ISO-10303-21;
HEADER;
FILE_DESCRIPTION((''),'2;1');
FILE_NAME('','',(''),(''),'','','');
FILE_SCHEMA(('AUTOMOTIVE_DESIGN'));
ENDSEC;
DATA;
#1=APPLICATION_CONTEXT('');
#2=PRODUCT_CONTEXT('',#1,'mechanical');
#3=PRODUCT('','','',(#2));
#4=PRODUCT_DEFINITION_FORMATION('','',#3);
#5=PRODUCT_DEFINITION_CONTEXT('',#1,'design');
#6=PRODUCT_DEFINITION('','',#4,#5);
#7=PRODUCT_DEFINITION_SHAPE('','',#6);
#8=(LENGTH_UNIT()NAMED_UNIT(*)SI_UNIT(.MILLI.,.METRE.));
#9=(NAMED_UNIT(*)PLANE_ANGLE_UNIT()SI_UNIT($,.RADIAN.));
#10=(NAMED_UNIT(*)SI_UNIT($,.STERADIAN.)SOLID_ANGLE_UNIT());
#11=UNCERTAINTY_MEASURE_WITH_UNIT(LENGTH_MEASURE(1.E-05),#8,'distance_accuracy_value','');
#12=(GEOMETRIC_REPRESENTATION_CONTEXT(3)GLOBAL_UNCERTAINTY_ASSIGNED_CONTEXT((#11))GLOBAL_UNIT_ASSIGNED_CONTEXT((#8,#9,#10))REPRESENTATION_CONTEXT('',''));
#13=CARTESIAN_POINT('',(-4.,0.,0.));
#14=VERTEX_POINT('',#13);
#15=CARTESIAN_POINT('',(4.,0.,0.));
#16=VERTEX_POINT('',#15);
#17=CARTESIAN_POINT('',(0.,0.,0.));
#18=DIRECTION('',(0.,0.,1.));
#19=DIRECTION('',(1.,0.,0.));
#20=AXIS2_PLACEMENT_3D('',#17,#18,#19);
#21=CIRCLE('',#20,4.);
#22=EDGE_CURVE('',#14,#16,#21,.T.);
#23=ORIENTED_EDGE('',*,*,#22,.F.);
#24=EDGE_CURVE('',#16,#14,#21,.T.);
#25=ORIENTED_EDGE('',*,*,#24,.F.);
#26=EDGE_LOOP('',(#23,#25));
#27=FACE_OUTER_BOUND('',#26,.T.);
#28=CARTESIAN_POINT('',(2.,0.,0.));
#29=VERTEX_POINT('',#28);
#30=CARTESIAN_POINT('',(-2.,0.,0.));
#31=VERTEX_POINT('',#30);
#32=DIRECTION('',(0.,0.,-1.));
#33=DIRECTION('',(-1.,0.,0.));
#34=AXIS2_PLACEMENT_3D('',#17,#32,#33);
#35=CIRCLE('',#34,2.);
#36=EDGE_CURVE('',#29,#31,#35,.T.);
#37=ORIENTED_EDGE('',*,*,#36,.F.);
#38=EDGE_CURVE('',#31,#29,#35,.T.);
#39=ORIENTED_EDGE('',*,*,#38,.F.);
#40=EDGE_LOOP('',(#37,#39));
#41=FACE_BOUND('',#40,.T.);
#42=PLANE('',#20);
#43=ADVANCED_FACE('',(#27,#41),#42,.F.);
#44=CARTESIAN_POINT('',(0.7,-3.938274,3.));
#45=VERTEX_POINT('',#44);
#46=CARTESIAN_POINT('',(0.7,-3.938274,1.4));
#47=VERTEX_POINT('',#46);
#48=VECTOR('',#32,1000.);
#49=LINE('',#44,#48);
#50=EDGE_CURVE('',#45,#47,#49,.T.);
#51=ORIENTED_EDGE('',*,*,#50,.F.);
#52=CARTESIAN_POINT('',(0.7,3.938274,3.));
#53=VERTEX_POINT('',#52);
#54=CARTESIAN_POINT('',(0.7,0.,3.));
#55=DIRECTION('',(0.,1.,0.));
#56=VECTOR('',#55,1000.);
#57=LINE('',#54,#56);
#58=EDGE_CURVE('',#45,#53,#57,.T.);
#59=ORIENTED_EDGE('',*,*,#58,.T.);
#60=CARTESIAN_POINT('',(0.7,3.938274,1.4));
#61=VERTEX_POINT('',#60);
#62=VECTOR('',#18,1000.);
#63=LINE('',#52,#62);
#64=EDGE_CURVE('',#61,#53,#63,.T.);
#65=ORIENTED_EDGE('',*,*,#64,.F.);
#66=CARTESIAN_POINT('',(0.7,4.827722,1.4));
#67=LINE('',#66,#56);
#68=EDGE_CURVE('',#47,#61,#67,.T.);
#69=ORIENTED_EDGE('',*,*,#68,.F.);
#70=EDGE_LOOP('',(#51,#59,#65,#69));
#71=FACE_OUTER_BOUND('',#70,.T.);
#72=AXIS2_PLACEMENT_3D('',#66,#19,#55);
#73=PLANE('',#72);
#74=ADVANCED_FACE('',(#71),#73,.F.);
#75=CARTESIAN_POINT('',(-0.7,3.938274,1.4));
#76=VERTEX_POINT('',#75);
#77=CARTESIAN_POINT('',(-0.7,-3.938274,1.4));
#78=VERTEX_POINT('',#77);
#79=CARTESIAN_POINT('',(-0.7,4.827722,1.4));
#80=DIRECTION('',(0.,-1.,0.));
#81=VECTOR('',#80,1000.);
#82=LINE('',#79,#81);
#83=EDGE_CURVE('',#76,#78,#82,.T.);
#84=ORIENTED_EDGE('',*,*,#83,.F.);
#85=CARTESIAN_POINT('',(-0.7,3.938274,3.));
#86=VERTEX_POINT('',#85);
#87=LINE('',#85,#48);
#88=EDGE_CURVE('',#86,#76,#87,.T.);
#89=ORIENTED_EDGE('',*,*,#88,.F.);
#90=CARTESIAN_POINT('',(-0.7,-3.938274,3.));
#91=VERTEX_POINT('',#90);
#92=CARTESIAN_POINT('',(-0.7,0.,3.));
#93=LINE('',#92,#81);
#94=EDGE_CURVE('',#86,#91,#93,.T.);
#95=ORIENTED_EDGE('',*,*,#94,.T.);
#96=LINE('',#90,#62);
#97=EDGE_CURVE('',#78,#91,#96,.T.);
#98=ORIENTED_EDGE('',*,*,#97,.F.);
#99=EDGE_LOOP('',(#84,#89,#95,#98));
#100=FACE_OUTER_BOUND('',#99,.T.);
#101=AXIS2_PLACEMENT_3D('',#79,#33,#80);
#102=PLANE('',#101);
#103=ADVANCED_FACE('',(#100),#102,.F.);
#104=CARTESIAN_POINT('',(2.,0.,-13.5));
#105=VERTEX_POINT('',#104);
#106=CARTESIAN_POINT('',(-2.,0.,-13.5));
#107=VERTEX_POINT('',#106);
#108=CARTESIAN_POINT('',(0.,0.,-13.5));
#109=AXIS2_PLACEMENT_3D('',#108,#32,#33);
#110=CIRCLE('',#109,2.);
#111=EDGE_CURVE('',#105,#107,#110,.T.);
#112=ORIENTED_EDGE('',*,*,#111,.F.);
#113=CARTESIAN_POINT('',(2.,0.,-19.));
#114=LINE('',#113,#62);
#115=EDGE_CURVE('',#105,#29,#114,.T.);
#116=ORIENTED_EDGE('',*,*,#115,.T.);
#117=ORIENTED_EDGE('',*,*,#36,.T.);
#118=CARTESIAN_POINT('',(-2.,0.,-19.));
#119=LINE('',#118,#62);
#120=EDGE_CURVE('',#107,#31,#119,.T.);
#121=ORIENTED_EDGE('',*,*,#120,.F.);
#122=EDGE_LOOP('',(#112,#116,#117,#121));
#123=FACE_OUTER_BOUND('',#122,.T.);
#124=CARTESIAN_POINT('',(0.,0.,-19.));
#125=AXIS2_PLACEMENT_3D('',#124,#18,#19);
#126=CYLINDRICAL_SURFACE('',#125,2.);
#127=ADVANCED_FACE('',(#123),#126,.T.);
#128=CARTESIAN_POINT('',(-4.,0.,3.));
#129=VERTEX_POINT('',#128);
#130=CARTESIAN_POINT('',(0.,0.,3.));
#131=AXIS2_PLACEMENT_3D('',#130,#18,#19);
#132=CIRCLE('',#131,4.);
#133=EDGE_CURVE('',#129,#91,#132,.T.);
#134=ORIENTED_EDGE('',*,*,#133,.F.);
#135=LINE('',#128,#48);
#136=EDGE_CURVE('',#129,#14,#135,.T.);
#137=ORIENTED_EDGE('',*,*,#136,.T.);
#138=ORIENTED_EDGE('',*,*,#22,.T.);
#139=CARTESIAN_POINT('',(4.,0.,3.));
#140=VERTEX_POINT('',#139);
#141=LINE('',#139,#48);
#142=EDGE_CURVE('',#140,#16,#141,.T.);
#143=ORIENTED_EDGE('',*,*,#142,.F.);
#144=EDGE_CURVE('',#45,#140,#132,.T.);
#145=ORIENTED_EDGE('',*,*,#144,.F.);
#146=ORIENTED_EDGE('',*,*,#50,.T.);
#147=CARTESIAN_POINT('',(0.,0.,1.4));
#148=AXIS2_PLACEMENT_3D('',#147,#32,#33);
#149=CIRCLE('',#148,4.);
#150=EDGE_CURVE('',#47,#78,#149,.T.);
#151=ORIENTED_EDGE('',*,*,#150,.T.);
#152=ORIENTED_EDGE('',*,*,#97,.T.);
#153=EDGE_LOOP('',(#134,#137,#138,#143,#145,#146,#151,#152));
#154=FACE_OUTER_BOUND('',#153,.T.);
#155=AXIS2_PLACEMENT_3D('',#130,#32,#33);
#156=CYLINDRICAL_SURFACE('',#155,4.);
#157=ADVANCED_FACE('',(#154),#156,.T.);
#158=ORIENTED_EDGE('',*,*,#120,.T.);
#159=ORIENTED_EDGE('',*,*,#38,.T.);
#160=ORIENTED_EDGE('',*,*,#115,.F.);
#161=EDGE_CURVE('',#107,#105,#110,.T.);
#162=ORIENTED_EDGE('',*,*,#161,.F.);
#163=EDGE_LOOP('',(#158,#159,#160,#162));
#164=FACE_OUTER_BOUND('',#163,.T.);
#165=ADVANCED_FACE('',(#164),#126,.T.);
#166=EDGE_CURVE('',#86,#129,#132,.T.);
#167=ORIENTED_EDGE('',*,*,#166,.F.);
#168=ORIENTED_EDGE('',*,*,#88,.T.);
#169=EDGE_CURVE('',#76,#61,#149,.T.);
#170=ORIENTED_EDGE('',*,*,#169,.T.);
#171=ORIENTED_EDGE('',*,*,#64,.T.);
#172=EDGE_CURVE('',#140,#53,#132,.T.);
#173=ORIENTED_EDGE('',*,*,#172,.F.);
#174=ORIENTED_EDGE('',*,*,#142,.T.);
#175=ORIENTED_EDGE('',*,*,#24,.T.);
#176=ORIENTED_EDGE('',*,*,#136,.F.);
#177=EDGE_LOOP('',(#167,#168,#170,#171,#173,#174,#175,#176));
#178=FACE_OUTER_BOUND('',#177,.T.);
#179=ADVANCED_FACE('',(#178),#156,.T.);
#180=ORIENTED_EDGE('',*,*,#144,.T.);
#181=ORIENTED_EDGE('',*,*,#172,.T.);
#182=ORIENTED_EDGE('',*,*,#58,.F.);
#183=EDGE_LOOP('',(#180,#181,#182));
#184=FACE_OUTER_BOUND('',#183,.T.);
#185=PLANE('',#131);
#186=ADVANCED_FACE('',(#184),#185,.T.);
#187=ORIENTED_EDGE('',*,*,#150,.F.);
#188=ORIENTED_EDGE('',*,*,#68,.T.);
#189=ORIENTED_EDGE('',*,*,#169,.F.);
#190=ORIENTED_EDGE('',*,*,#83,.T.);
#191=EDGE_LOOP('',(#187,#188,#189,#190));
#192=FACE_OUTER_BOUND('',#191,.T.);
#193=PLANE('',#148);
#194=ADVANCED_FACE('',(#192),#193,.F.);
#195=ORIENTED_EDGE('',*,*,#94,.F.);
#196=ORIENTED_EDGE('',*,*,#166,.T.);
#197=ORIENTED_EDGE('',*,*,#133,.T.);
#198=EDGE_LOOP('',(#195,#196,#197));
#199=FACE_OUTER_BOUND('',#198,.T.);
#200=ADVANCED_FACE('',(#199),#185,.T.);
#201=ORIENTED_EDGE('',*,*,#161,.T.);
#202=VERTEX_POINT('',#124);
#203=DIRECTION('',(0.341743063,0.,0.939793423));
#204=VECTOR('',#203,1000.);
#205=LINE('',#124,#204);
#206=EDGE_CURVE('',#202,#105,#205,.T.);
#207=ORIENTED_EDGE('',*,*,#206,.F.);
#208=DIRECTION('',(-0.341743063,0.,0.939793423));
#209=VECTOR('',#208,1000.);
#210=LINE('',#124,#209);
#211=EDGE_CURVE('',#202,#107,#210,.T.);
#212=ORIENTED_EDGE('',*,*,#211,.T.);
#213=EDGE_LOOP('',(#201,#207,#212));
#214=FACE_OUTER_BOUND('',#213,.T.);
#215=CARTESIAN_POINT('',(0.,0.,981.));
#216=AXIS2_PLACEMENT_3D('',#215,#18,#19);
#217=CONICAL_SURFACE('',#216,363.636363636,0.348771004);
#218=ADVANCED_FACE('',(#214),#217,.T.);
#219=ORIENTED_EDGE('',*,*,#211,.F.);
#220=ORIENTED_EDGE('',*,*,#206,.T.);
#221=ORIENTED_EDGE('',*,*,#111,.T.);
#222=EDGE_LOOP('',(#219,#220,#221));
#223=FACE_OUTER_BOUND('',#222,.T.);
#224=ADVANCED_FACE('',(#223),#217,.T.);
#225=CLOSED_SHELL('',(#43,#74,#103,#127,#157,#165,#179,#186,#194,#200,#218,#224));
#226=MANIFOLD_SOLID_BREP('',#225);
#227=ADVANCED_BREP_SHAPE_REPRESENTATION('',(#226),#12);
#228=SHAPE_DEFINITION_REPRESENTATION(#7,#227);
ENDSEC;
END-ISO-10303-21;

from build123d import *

# Parameters (mm, degrees)
SKETCH1_R           = 4
BOSS_EXTRUDE1_DEPTH = 3
SKETCH2_W           = 1.4
SKETCH2_H           = 9.655444372
CUT_EXTRUDE1_DEPTH  = 1.6
SKETCH3_R           = 2
BOSS_EXTRUDE2_DEPTH = 19


with BuildPart() as part:
    # Sketch1 → Boss-Extrude1 (new body)
    with BuildSketch(Plane.XY):
        Circle(SKETCH1_R)
    extrude(amount=BOSS_EXTRUDE1_DEPTH)

    # Sketch2 → Cut-Extrude1 (cut)
    with BuildSketch(Plane.XY.offset(3)):
        Rectangle(SKETCH2_W, SKETCH2_H)
    extrude(amount=-CUT_EXTRUDE1_DEPTH, mode=Mode.SUBTRACT)

    # Sketch3 → Boss-Extrude2 (add)
    with BuildSketch(Plane(origin=(0, 0, 0), x_dir=(-1, 0, 0), z_dir=(0, 0, -1))):
        Circle(SKETCH3_R)
    extrude(amount=BOSS_EXTRUDE2_DEPTH)

    # Sketch4 → Cut-Revolve5 (revolve, cut)
    with BuildSketch(Plane(origin=(0, 0, 0), x_dir=(1, 0, 0), z_dir=(0, 1, 0)), mode=Mode.PRIVATE) as cut_revolve5_sk:
        Polygon((2, 13.5), (2, 19), (0, 26.182661303), (0, 19), align=None)
    revolve(cut_revolve5_sk.sketch.rotate(Axis((0, 0, -19), (0, 0, 1)), 100.078658108), axis=Axis((0, 0, -19), (0, 0, 1)), mode=Mode.SUBTRACT)


solid = part.part
